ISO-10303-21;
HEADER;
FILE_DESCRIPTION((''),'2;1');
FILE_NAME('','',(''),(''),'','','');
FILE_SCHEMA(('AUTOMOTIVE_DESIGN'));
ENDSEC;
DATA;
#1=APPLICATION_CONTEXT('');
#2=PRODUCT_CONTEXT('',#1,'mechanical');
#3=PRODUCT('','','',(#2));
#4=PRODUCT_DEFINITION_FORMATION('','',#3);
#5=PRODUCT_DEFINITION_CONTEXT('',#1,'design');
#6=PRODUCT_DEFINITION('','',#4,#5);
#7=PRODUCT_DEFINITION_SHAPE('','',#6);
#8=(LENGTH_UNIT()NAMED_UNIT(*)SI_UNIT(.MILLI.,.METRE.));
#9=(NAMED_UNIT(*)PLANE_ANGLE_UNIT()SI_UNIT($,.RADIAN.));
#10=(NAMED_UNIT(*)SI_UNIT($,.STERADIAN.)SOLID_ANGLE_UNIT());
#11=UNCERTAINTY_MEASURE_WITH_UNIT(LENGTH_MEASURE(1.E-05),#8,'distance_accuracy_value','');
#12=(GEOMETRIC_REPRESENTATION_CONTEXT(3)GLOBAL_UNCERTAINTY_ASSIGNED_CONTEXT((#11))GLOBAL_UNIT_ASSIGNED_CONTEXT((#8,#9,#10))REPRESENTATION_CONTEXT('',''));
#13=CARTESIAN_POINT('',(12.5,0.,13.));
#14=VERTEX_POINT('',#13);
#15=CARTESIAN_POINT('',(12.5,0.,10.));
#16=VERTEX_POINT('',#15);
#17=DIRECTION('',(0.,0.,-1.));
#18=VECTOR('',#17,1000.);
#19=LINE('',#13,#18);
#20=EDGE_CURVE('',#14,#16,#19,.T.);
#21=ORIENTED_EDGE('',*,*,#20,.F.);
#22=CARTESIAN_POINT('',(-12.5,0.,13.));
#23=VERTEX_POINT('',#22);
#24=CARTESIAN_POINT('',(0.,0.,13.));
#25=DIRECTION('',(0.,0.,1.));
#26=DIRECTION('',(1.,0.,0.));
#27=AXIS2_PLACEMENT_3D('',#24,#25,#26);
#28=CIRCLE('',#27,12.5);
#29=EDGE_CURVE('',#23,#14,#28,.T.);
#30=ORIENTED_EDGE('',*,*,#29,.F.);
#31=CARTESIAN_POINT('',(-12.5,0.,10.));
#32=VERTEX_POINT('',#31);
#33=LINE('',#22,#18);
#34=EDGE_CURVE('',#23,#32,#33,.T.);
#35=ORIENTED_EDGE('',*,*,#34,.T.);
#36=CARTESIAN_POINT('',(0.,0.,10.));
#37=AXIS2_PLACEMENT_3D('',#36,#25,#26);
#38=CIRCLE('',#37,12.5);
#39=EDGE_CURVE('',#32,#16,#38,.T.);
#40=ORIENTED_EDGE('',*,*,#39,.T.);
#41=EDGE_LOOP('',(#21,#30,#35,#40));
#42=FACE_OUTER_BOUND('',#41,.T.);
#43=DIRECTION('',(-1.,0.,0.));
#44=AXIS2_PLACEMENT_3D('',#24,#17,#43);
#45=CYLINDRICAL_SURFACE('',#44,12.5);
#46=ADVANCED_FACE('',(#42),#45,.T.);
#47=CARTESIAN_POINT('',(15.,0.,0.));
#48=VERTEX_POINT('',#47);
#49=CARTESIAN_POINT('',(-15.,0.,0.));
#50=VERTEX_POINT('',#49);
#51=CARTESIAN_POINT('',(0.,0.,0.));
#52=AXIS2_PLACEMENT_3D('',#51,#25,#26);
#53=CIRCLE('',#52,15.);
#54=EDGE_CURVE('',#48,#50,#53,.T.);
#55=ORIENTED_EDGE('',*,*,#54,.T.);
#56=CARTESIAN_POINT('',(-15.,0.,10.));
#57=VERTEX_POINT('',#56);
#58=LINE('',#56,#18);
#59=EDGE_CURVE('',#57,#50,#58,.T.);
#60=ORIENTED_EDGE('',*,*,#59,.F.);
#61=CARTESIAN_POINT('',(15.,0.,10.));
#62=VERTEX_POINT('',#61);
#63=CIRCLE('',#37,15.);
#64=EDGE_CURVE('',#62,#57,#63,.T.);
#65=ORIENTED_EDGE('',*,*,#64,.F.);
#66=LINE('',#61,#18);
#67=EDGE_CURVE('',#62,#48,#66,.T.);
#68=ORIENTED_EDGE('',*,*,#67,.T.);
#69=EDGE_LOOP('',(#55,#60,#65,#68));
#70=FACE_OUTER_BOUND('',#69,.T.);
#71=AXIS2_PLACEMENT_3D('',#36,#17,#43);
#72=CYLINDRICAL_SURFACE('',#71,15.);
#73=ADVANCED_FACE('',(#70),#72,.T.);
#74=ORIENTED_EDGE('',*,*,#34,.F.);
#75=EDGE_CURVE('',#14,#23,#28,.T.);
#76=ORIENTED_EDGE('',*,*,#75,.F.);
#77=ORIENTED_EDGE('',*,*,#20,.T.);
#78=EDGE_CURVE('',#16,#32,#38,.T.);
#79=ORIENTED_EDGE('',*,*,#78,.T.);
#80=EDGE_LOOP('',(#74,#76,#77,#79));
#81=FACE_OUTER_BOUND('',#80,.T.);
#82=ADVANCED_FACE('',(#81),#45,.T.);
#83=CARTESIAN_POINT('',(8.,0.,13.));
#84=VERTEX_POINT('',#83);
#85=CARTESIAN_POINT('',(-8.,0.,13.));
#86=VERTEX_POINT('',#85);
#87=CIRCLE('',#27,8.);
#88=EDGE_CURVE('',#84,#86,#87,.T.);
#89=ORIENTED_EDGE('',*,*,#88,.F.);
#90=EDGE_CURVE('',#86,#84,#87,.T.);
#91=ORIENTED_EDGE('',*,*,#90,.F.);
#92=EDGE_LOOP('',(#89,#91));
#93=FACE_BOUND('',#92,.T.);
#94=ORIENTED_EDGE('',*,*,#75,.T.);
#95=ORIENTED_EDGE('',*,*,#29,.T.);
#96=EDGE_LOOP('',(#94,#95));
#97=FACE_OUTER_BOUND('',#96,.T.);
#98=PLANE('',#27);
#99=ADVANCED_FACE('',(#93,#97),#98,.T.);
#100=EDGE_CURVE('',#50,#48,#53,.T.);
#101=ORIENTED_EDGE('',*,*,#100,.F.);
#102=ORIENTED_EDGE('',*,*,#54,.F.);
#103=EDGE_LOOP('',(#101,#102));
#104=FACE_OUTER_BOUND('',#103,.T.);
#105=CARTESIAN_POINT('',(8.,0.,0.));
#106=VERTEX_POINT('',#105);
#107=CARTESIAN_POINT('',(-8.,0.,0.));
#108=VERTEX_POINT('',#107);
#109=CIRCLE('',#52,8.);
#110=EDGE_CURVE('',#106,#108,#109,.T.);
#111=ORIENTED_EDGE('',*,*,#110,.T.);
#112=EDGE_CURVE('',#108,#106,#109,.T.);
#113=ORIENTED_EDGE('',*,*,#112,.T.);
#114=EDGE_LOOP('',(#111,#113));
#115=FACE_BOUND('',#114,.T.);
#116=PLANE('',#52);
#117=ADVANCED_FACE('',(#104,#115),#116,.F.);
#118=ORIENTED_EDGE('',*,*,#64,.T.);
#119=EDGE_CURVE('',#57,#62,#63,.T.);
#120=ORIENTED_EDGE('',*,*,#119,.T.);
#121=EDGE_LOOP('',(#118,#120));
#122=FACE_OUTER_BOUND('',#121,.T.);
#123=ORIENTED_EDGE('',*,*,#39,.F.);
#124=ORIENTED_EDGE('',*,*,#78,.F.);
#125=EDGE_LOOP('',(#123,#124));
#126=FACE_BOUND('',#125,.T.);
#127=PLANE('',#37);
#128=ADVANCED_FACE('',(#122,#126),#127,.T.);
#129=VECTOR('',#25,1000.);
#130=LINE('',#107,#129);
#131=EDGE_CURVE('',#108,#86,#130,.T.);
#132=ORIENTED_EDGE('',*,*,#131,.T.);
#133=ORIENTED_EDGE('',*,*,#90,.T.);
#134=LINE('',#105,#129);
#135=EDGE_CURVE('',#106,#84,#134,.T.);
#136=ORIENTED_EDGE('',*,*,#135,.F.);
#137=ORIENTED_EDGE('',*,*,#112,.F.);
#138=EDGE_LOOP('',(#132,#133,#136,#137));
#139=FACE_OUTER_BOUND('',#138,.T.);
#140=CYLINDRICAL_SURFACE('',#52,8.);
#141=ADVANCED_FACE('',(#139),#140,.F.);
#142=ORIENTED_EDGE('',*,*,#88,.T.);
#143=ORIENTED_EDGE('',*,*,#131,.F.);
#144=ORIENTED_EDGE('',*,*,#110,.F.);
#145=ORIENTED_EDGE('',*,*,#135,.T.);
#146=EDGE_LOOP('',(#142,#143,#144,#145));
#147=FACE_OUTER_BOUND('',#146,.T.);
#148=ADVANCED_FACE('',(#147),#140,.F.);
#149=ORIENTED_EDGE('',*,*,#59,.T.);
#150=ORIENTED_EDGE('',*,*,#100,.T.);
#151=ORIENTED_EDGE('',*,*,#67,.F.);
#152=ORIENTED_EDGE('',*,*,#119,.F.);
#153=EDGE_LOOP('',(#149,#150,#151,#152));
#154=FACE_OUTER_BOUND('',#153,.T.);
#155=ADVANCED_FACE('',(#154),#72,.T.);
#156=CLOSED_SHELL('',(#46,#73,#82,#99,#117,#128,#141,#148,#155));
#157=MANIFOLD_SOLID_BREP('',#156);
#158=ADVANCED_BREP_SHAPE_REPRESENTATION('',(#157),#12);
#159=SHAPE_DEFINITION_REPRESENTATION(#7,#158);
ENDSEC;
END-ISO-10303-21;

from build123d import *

# Parameters (mm, degrees)
SKETCH1_R           = 15
BOSS_EXTRUDE1_DEPTH = 10
SKETCH2_R           = 12.5
BOSS_EXTRUDE2_DEPTH = 3
SKETCH3_R           = 8
CUT_EXTRUDE1_DEPTH  = 25.879710609


with BuildPart() as part:
    # Sketch1 → Boss-Extrude1 (new body)
    with BuildSketch(Plane.XY):
        Circle(SKETCH1_R)
    extrude(amount=BOSS_EXTRUDE1_DEPTH)

    # Sketch2 → Boss-Extrude2 (add)
    with BuildSketch(Plane.XY.offset(10)):
        Circle(SKETCH2_R)
    extrude(amount=BOSS_EXTRUDE2_DEPTH)

    # Sketch3 → Cut-Extrude1 (cut, through all)
    with BuildSketch(Plane.XY.offset(13)):
        Circle(SKETCH3_R)
    extrude(amount=-CUT_EXTRUDE1_DEPTH, mode=Mode.SUBTRACT)


solid = part.part
